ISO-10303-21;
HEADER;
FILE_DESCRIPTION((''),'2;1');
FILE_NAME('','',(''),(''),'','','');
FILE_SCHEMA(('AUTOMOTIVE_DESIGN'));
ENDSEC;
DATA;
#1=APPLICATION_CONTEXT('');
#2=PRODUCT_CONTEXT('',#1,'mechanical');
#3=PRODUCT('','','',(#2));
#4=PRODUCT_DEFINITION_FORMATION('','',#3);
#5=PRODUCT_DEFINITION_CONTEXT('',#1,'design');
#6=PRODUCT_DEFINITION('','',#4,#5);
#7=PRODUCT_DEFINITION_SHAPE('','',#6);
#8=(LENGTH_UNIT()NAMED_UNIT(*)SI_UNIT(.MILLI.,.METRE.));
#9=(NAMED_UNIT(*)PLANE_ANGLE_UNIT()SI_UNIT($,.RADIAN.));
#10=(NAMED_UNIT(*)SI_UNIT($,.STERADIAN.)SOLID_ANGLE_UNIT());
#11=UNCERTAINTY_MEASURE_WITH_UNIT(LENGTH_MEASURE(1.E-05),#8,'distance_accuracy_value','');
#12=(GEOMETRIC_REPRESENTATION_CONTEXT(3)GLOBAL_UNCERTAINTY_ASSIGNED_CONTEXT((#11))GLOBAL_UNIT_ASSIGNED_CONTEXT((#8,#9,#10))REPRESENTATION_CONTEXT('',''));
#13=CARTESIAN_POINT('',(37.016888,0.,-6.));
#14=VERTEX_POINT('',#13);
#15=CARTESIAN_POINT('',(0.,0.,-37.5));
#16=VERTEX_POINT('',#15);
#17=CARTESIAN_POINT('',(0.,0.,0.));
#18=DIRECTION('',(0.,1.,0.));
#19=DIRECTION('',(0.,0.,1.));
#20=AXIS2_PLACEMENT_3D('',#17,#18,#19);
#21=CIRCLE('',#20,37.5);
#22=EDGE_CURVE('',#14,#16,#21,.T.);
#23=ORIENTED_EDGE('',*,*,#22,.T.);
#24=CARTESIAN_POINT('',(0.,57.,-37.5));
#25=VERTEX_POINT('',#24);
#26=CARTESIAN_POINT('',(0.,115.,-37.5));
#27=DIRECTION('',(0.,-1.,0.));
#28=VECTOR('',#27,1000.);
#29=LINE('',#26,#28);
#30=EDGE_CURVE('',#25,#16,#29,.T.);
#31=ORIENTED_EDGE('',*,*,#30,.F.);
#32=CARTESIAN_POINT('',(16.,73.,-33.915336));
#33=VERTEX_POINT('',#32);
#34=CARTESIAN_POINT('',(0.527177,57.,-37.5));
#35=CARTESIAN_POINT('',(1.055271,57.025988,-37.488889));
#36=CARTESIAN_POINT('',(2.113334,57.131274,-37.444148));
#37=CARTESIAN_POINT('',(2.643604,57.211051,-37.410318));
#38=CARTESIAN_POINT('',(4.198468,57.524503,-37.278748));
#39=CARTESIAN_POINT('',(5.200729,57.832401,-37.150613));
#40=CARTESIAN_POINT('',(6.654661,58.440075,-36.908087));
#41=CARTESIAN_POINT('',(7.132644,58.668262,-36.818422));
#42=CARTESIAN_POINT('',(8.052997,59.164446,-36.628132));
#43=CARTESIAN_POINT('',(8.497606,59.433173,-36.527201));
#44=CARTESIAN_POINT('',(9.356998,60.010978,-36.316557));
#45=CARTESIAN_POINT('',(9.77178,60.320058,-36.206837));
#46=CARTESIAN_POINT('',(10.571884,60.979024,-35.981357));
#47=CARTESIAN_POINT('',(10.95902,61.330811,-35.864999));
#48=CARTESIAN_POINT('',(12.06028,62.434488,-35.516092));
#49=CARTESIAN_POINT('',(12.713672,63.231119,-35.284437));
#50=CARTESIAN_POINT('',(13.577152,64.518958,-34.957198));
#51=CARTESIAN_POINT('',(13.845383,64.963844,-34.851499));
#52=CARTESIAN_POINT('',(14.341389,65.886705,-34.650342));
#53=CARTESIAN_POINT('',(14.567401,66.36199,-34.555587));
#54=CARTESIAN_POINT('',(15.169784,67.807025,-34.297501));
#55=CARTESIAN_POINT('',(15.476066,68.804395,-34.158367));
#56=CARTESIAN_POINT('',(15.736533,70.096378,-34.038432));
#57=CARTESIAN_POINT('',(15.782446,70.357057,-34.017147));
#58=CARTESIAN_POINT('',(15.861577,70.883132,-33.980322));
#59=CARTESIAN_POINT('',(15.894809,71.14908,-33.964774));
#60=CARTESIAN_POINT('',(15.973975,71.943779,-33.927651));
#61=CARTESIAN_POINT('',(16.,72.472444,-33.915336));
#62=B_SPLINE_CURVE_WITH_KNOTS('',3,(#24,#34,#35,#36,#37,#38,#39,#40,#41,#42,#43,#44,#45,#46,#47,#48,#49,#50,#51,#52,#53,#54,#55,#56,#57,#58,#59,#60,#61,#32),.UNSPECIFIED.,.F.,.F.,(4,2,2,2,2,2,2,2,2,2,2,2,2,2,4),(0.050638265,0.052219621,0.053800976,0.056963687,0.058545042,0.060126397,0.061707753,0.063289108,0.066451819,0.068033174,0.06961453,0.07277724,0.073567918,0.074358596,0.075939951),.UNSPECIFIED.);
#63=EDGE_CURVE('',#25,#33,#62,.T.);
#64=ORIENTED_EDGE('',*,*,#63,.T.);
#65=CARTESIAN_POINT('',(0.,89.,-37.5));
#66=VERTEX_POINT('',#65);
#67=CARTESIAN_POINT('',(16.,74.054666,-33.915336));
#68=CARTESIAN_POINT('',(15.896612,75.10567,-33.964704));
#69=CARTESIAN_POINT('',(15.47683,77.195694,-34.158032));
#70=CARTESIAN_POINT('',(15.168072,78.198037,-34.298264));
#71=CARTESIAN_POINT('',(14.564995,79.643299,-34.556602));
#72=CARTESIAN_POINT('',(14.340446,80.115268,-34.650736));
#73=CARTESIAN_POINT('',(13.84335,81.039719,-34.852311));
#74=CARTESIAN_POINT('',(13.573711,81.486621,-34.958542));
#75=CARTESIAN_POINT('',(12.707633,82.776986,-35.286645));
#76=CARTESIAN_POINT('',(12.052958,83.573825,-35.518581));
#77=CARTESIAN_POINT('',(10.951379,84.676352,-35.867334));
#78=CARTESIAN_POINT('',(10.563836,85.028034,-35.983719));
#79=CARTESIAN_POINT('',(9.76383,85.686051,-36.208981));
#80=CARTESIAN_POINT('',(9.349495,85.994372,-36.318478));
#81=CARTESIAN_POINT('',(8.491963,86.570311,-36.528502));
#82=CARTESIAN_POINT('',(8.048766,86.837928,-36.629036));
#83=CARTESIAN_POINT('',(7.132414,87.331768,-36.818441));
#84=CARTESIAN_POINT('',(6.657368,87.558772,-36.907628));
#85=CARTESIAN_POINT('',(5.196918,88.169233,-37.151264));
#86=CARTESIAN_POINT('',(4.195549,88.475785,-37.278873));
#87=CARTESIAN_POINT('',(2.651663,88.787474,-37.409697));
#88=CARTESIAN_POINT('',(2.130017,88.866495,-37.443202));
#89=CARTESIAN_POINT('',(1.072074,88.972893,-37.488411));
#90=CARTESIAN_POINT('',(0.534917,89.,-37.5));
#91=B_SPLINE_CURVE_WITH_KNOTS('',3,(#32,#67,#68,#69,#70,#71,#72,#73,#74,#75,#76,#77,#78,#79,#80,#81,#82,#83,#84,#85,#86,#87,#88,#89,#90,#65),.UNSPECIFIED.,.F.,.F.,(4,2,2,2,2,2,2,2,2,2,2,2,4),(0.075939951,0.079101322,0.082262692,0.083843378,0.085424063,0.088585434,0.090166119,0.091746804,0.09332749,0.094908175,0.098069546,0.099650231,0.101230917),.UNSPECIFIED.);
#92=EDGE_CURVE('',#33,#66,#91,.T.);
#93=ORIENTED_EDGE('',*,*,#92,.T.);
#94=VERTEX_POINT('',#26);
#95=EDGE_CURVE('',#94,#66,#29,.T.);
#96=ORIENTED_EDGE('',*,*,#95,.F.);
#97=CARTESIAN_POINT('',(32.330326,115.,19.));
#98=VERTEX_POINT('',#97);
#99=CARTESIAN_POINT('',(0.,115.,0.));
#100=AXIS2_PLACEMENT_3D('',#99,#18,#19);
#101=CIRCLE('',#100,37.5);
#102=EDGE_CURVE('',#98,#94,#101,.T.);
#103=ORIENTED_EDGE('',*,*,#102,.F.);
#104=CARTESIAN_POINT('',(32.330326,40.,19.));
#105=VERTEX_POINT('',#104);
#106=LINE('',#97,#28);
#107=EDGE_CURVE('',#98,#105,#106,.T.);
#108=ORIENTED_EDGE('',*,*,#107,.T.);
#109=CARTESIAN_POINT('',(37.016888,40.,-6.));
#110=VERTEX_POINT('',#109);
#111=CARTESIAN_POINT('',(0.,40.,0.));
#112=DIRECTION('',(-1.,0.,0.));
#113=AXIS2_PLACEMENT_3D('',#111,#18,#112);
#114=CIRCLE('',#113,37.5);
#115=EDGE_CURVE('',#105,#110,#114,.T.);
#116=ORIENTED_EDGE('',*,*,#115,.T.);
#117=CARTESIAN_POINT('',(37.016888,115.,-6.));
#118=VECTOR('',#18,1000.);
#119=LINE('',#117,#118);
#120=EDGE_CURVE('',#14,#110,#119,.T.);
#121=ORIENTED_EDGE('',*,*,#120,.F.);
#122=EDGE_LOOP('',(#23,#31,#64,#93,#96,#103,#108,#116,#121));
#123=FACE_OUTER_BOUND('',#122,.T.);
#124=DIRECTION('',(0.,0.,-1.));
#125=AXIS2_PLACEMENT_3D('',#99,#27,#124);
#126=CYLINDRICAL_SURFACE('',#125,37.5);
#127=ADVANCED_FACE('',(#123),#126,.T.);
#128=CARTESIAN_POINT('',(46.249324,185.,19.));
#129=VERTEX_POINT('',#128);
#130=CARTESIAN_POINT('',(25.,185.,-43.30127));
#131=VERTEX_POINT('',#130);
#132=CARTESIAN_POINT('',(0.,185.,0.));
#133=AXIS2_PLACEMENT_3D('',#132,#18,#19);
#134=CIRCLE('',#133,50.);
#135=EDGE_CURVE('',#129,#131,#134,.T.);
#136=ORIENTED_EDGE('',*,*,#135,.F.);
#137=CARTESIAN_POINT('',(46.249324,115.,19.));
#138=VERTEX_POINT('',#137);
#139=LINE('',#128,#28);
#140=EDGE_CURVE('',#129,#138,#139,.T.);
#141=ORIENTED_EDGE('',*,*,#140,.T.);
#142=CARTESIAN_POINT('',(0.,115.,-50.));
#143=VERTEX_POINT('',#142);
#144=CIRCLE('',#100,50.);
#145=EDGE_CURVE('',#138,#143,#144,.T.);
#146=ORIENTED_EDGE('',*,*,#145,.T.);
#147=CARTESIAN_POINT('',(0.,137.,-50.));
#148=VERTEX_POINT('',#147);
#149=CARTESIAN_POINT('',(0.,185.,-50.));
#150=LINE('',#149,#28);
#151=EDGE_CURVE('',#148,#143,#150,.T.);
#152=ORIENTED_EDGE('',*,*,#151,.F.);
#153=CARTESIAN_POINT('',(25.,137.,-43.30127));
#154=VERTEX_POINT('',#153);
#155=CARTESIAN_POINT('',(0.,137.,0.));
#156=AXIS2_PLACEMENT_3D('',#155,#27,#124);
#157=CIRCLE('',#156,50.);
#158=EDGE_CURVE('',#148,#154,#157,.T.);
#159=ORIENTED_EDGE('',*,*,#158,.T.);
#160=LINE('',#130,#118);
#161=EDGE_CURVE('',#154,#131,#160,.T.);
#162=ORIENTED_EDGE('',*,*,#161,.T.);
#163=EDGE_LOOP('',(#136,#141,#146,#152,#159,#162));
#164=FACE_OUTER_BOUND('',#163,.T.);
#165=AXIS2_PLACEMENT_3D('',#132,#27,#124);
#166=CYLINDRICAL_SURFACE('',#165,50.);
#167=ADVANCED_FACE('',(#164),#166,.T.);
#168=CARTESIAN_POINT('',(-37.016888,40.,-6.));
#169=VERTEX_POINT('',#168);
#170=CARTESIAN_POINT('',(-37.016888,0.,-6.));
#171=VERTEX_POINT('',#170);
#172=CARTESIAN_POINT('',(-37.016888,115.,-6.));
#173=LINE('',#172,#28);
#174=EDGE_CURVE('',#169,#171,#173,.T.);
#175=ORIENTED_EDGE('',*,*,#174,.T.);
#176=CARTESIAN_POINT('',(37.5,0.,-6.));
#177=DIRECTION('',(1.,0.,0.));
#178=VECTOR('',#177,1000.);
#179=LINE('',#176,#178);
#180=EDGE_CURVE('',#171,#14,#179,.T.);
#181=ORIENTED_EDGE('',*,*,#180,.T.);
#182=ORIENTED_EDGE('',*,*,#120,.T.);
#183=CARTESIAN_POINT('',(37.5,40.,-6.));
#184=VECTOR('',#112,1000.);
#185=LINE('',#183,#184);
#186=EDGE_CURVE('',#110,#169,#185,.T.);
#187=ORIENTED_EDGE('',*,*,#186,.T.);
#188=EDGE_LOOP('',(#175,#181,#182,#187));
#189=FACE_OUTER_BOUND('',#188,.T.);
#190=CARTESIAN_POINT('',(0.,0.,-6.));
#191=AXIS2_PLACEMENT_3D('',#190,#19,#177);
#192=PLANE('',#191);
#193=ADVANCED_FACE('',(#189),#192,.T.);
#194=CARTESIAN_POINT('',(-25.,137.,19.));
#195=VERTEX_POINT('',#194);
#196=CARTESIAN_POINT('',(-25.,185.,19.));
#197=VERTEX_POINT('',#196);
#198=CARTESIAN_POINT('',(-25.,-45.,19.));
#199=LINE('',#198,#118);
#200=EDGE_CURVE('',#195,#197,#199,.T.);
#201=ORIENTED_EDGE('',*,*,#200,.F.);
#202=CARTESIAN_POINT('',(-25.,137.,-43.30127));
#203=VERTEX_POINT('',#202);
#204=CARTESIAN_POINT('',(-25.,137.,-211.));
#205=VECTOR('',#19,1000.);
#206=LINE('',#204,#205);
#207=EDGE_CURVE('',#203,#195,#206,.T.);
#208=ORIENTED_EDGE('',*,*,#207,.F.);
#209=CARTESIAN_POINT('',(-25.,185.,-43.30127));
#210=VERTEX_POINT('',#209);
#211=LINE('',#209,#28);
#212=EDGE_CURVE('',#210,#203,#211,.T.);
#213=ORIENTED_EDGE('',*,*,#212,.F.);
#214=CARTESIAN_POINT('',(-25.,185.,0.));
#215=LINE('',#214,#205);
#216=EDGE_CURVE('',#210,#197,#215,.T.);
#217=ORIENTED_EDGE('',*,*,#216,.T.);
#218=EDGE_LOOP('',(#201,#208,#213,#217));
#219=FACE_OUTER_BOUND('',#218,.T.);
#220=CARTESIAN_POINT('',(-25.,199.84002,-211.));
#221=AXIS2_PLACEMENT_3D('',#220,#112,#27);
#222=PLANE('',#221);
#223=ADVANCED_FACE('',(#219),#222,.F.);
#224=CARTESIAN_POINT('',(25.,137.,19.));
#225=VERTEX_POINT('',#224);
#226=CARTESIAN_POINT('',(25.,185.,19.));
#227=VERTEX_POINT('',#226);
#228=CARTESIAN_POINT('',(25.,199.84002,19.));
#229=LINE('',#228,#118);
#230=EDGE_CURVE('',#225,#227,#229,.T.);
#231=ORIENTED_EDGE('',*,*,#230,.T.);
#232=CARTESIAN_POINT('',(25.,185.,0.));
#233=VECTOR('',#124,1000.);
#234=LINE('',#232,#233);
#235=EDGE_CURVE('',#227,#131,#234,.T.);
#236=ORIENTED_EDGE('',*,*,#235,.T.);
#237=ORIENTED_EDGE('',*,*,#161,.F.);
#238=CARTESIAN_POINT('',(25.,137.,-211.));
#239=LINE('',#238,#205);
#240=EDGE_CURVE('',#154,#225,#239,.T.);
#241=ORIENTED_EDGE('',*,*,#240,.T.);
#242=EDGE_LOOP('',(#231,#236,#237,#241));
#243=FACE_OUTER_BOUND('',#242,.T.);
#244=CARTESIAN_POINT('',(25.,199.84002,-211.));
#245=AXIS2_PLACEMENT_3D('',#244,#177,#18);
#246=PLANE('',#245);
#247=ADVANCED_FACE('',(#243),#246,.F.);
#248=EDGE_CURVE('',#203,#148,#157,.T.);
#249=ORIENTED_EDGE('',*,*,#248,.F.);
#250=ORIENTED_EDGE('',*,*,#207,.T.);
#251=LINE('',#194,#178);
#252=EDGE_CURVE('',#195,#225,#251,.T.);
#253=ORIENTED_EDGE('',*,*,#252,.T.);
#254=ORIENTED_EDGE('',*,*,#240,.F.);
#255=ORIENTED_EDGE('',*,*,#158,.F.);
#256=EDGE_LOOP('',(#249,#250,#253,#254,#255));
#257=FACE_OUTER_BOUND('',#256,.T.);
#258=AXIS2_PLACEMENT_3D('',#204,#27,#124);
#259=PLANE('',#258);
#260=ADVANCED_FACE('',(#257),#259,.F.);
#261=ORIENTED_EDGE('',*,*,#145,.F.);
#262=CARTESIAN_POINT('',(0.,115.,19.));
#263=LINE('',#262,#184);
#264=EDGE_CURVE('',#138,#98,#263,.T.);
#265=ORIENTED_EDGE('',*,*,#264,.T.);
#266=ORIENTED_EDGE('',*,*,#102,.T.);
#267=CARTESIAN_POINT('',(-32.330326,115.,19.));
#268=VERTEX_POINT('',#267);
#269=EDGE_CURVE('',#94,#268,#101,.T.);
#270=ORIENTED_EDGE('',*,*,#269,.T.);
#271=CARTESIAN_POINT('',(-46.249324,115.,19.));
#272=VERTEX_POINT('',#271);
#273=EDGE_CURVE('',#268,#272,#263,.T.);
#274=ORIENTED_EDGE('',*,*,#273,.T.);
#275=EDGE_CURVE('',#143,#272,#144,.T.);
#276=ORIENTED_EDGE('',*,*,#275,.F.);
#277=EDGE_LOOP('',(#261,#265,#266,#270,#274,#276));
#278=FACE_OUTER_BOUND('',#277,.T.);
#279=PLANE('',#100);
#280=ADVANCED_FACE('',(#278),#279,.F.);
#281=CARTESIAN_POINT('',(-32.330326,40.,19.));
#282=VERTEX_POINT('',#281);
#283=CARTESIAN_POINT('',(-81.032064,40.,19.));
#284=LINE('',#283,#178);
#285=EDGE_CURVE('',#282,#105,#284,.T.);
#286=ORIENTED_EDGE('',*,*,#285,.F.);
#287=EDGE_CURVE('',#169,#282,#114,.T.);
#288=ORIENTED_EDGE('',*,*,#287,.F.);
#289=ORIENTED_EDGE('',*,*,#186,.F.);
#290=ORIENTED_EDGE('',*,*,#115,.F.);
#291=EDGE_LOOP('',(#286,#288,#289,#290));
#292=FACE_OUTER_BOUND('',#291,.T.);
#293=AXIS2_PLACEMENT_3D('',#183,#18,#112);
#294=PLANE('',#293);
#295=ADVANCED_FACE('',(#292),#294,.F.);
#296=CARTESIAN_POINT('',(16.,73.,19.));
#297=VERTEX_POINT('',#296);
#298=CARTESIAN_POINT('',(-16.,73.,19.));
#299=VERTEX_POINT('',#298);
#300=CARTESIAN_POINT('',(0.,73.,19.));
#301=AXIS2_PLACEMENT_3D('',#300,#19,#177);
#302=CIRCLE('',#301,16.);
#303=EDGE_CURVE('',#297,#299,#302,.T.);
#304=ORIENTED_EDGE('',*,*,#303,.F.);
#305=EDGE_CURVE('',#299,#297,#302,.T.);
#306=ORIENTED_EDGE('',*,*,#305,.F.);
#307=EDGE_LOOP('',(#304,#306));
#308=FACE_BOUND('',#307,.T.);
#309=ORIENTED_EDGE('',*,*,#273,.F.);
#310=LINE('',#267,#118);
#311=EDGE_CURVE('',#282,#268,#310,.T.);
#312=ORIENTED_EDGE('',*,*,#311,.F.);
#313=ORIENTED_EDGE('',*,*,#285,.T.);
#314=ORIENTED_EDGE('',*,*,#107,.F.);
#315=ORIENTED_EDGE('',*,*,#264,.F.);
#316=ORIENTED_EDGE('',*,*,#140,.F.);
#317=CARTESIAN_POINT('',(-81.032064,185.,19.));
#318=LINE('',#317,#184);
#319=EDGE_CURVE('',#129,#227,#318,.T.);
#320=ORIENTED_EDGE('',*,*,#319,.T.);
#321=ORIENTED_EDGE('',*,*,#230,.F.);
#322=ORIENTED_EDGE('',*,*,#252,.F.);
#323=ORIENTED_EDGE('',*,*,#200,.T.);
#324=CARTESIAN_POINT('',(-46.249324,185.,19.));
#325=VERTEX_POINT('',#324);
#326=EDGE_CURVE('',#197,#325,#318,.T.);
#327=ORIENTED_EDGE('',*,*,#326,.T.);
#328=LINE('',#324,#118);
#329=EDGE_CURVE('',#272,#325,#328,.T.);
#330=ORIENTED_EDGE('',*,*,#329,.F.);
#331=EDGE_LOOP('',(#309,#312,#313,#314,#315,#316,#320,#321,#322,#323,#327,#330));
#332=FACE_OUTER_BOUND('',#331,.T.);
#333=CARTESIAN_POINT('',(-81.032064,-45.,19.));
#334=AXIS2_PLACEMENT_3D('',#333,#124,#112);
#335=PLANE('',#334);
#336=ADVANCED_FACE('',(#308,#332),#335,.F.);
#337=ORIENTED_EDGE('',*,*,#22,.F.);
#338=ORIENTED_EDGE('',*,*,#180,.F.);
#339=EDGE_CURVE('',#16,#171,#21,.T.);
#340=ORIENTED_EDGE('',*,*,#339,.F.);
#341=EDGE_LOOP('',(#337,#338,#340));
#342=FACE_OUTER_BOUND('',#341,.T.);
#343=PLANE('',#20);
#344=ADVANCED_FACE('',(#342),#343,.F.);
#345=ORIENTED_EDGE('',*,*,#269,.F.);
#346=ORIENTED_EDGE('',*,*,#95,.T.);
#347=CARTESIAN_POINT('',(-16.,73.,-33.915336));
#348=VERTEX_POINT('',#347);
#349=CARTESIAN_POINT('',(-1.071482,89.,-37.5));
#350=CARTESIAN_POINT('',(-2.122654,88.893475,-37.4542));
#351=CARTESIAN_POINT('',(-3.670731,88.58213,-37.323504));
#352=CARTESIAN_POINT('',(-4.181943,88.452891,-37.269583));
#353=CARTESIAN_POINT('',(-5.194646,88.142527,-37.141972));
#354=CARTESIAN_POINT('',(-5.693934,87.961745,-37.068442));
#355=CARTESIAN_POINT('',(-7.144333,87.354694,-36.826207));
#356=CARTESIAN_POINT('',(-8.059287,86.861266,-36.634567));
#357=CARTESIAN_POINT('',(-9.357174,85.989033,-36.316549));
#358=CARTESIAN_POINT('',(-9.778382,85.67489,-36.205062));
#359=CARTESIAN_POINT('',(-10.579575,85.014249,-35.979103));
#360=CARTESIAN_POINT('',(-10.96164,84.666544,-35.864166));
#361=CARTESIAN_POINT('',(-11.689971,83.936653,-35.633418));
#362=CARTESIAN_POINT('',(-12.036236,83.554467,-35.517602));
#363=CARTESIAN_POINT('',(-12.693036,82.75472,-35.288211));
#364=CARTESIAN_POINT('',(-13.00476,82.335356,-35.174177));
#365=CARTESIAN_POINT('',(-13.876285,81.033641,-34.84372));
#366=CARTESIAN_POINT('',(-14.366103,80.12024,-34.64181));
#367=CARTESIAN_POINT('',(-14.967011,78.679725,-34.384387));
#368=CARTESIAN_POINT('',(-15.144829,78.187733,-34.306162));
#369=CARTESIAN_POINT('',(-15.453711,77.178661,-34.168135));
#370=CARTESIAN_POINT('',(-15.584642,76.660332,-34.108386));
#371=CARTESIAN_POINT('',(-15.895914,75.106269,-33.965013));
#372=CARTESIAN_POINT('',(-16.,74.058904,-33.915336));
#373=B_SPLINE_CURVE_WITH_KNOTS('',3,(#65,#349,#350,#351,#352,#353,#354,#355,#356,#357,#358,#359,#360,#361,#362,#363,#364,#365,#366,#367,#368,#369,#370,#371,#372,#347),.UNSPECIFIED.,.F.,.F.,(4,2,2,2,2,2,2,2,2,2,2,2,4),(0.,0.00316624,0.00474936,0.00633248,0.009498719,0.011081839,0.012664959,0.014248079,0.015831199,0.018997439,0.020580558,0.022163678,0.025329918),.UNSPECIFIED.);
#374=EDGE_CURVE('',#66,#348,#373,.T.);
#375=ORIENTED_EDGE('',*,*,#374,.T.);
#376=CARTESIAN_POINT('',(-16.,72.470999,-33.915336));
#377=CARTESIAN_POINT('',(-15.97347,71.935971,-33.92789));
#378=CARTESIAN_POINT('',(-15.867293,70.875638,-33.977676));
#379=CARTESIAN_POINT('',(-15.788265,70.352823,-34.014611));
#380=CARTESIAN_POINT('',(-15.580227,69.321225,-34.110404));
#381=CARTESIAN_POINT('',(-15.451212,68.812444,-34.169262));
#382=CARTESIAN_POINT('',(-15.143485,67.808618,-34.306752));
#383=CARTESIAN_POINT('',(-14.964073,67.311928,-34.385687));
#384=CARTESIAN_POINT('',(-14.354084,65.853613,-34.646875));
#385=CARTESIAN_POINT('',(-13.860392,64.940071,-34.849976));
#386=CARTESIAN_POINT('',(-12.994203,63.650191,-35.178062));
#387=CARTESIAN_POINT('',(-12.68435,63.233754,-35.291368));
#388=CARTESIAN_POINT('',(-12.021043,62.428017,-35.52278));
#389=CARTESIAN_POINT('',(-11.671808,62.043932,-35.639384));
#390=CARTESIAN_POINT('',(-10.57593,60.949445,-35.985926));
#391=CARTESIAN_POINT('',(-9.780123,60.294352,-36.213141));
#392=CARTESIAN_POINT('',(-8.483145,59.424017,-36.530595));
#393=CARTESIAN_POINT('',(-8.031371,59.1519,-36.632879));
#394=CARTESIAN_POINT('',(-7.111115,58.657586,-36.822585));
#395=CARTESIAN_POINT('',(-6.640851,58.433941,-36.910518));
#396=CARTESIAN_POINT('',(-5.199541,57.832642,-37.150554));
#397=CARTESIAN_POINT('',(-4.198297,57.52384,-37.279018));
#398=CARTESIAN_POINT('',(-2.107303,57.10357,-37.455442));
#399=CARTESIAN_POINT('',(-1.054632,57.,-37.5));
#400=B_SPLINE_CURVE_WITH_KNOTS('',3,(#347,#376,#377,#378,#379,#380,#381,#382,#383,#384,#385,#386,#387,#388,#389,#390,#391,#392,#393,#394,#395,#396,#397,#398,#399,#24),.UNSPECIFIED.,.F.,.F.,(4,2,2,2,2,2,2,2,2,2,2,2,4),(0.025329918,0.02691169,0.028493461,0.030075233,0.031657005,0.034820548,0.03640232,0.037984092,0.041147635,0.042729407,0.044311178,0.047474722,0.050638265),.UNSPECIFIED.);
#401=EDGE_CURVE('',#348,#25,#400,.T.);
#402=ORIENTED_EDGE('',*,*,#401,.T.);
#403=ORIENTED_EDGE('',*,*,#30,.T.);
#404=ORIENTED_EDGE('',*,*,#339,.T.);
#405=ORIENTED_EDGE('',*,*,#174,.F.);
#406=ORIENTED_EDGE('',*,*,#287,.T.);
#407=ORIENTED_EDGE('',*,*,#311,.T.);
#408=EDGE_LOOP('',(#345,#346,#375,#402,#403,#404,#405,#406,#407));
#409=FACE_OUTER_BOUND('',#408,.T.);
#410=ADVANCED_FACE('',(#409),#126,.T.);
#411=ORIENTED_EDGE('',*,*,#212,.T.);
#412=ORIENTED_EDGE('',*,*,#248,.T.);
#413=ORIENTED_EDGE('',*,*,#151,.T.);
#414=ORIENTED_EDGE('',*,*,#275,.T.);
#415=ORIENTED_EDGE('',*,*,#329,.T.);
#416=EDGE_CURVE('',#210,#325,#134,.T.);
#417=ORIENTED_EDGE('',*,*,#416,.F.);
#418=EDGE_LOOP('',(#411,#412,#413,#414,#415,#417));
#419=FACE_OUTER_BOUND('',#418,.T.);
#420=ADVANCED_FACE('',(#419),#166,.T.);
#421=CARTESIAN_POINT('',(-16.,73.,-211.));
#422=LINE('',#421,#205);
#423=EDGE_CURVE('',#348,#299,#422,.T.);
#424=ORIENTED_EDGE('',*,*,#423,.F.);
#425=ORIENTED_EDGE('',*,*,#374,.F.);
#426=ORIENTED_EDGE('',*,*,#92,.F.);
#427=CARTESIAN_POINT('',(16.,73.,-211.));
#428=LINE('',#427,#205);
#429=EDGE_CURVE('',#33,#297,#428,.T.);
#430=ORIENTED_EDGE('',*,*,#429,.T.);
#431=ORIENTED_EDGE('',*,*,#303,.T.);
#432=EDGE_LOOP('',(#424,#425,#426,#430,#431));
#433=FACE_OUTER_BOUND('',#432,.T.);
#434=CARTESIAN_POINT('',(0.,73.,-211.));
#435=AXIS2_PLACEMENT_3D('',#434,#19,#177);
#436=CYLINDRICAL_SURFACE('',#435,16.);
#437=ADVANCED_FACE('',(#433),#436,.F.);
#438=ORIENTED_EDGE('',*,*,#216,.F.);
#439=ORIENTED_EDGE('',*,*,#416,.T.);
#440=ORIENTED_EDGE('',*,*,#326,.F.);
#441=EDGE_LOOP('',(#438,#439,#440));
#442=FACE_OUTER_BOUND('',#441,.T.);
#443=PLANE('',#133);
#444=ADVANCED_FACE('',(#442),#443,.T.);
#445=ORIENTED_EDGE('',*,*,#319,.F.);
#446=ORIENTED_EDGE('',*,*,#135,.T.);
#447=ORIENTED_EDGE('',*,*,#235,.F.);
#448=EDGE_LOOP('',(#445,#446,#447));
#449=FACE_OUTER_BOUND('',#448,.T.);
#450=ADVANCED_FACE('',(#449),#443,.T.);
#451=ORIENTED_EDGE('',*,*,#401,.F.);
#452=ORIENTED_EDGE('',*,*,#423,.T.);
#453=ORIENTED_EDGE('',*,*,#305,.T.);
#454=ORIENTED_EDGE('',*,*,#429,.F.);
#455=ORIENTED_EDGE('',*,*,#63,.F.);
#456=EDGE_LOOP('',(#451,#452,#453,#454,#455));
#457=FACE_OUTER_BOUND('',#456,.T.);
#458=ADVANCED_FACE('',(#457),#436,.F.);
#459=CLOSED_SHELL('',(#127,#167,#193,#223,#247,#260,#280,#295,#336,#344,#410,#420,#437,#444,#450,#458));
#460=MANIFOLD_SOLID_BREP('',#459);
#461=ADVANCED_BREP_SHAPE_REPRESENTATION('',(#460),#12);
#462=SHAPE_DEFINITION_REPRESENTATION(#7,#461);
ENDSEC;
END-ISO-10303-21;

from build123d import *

# Parameters (mm, degrees)
SHANK_PROFILE_75_R   = 37.5
SHANK_75_DEPTH       = 115
HEAD_PROFILE_100_R   = 50
FORK_HEAD_100_DEPTH  = 70
FLAT_FACE_CUT_DEPTH  = 230
FORK_SLOT_PROFILE_R  = 16
FORK_SLOT_PROFILE_W  = 50
FORK_SLOT_PROFILE_H  = 62.840020357
FORK_SLOT_CUT_DEPTH  = 230
CROSS_HOLE_PROFILE_W = 75
CROSS_HOLE_PROFILE_H = 40
CROSS_HOLE_CUT_DEPTH = 25


with BuildPart() as part:
    # Shank Profile Ø75 → Shank Ø75 (new body)
    with BuildSketch(Plane(origin=(0, 0, 0), x_dir=(1, 0, 0), z_dir=(0, 1, 0))):
        with Locations(Location((0, 0, 0), (0, 0, 270))):
            Circle(SHANK_PROFILE_75_R)
    extrude(amount=SHANK_75_DEPTH)

    # Head Profile Ø100 → Fork Head Ø100 (add)
    with BuildSketch(Plane(origin=(0, 115, 0), x_dir=(1, 0, 0), z_dir=(0, 1, 0))):
        with Locations(Location((0, 0, 0), (0, 0, 270))):
            Circle(HEAD_PROFILE_100_R)
    extrude(amount=FORK_HEAD_100_DEPTH)

    # Flat Face Profile → Flat Face Cut (cut)
    with BuildSketch(Plane(origin=(0, 185, 0), x_dir=(1, 0, 0), z_dir=(0, 1, 0))):
        Polygon((-81.032063785, -19), (77.121249896, -19), (5.631572001, -69.155704166), align=None)
    extrude(amount=-FLAT_FACE_CUT_DEPTH, mode=Mode.SUBTRACT)

    # Fork Slot Profile → Fork Slot Cut (cut)
    with BuildSketch(Plane.XY.offset(19)):
        with Locations((0, 73)):
            Circle(FORK_SLOT_PROFILE_R)
        with Locations((0, 168.420010179)):
            Rectangle(FORK_SLOT_PROFILE_W, FORK_SLOT_PROFILE_H)
    extrude(amount=-FORK_SLOT_CUT_DEPTH, mode=Mode.SUBTRACT)

    # Cross Hole Profile → Cross Hole Cut (cut)
    with BuildSketch(Plane.XY.offset(19)):
        with Locations((0, 20)):
            Rectangle(CROSS_HOLE_PROFILE_W, CROSS_HOLE_PROFILE_H)
    extrude(amount=-CROSS_HOLE_CUT_DEPTH, mode=Mode.SUBTRACT)


solid = part.part
